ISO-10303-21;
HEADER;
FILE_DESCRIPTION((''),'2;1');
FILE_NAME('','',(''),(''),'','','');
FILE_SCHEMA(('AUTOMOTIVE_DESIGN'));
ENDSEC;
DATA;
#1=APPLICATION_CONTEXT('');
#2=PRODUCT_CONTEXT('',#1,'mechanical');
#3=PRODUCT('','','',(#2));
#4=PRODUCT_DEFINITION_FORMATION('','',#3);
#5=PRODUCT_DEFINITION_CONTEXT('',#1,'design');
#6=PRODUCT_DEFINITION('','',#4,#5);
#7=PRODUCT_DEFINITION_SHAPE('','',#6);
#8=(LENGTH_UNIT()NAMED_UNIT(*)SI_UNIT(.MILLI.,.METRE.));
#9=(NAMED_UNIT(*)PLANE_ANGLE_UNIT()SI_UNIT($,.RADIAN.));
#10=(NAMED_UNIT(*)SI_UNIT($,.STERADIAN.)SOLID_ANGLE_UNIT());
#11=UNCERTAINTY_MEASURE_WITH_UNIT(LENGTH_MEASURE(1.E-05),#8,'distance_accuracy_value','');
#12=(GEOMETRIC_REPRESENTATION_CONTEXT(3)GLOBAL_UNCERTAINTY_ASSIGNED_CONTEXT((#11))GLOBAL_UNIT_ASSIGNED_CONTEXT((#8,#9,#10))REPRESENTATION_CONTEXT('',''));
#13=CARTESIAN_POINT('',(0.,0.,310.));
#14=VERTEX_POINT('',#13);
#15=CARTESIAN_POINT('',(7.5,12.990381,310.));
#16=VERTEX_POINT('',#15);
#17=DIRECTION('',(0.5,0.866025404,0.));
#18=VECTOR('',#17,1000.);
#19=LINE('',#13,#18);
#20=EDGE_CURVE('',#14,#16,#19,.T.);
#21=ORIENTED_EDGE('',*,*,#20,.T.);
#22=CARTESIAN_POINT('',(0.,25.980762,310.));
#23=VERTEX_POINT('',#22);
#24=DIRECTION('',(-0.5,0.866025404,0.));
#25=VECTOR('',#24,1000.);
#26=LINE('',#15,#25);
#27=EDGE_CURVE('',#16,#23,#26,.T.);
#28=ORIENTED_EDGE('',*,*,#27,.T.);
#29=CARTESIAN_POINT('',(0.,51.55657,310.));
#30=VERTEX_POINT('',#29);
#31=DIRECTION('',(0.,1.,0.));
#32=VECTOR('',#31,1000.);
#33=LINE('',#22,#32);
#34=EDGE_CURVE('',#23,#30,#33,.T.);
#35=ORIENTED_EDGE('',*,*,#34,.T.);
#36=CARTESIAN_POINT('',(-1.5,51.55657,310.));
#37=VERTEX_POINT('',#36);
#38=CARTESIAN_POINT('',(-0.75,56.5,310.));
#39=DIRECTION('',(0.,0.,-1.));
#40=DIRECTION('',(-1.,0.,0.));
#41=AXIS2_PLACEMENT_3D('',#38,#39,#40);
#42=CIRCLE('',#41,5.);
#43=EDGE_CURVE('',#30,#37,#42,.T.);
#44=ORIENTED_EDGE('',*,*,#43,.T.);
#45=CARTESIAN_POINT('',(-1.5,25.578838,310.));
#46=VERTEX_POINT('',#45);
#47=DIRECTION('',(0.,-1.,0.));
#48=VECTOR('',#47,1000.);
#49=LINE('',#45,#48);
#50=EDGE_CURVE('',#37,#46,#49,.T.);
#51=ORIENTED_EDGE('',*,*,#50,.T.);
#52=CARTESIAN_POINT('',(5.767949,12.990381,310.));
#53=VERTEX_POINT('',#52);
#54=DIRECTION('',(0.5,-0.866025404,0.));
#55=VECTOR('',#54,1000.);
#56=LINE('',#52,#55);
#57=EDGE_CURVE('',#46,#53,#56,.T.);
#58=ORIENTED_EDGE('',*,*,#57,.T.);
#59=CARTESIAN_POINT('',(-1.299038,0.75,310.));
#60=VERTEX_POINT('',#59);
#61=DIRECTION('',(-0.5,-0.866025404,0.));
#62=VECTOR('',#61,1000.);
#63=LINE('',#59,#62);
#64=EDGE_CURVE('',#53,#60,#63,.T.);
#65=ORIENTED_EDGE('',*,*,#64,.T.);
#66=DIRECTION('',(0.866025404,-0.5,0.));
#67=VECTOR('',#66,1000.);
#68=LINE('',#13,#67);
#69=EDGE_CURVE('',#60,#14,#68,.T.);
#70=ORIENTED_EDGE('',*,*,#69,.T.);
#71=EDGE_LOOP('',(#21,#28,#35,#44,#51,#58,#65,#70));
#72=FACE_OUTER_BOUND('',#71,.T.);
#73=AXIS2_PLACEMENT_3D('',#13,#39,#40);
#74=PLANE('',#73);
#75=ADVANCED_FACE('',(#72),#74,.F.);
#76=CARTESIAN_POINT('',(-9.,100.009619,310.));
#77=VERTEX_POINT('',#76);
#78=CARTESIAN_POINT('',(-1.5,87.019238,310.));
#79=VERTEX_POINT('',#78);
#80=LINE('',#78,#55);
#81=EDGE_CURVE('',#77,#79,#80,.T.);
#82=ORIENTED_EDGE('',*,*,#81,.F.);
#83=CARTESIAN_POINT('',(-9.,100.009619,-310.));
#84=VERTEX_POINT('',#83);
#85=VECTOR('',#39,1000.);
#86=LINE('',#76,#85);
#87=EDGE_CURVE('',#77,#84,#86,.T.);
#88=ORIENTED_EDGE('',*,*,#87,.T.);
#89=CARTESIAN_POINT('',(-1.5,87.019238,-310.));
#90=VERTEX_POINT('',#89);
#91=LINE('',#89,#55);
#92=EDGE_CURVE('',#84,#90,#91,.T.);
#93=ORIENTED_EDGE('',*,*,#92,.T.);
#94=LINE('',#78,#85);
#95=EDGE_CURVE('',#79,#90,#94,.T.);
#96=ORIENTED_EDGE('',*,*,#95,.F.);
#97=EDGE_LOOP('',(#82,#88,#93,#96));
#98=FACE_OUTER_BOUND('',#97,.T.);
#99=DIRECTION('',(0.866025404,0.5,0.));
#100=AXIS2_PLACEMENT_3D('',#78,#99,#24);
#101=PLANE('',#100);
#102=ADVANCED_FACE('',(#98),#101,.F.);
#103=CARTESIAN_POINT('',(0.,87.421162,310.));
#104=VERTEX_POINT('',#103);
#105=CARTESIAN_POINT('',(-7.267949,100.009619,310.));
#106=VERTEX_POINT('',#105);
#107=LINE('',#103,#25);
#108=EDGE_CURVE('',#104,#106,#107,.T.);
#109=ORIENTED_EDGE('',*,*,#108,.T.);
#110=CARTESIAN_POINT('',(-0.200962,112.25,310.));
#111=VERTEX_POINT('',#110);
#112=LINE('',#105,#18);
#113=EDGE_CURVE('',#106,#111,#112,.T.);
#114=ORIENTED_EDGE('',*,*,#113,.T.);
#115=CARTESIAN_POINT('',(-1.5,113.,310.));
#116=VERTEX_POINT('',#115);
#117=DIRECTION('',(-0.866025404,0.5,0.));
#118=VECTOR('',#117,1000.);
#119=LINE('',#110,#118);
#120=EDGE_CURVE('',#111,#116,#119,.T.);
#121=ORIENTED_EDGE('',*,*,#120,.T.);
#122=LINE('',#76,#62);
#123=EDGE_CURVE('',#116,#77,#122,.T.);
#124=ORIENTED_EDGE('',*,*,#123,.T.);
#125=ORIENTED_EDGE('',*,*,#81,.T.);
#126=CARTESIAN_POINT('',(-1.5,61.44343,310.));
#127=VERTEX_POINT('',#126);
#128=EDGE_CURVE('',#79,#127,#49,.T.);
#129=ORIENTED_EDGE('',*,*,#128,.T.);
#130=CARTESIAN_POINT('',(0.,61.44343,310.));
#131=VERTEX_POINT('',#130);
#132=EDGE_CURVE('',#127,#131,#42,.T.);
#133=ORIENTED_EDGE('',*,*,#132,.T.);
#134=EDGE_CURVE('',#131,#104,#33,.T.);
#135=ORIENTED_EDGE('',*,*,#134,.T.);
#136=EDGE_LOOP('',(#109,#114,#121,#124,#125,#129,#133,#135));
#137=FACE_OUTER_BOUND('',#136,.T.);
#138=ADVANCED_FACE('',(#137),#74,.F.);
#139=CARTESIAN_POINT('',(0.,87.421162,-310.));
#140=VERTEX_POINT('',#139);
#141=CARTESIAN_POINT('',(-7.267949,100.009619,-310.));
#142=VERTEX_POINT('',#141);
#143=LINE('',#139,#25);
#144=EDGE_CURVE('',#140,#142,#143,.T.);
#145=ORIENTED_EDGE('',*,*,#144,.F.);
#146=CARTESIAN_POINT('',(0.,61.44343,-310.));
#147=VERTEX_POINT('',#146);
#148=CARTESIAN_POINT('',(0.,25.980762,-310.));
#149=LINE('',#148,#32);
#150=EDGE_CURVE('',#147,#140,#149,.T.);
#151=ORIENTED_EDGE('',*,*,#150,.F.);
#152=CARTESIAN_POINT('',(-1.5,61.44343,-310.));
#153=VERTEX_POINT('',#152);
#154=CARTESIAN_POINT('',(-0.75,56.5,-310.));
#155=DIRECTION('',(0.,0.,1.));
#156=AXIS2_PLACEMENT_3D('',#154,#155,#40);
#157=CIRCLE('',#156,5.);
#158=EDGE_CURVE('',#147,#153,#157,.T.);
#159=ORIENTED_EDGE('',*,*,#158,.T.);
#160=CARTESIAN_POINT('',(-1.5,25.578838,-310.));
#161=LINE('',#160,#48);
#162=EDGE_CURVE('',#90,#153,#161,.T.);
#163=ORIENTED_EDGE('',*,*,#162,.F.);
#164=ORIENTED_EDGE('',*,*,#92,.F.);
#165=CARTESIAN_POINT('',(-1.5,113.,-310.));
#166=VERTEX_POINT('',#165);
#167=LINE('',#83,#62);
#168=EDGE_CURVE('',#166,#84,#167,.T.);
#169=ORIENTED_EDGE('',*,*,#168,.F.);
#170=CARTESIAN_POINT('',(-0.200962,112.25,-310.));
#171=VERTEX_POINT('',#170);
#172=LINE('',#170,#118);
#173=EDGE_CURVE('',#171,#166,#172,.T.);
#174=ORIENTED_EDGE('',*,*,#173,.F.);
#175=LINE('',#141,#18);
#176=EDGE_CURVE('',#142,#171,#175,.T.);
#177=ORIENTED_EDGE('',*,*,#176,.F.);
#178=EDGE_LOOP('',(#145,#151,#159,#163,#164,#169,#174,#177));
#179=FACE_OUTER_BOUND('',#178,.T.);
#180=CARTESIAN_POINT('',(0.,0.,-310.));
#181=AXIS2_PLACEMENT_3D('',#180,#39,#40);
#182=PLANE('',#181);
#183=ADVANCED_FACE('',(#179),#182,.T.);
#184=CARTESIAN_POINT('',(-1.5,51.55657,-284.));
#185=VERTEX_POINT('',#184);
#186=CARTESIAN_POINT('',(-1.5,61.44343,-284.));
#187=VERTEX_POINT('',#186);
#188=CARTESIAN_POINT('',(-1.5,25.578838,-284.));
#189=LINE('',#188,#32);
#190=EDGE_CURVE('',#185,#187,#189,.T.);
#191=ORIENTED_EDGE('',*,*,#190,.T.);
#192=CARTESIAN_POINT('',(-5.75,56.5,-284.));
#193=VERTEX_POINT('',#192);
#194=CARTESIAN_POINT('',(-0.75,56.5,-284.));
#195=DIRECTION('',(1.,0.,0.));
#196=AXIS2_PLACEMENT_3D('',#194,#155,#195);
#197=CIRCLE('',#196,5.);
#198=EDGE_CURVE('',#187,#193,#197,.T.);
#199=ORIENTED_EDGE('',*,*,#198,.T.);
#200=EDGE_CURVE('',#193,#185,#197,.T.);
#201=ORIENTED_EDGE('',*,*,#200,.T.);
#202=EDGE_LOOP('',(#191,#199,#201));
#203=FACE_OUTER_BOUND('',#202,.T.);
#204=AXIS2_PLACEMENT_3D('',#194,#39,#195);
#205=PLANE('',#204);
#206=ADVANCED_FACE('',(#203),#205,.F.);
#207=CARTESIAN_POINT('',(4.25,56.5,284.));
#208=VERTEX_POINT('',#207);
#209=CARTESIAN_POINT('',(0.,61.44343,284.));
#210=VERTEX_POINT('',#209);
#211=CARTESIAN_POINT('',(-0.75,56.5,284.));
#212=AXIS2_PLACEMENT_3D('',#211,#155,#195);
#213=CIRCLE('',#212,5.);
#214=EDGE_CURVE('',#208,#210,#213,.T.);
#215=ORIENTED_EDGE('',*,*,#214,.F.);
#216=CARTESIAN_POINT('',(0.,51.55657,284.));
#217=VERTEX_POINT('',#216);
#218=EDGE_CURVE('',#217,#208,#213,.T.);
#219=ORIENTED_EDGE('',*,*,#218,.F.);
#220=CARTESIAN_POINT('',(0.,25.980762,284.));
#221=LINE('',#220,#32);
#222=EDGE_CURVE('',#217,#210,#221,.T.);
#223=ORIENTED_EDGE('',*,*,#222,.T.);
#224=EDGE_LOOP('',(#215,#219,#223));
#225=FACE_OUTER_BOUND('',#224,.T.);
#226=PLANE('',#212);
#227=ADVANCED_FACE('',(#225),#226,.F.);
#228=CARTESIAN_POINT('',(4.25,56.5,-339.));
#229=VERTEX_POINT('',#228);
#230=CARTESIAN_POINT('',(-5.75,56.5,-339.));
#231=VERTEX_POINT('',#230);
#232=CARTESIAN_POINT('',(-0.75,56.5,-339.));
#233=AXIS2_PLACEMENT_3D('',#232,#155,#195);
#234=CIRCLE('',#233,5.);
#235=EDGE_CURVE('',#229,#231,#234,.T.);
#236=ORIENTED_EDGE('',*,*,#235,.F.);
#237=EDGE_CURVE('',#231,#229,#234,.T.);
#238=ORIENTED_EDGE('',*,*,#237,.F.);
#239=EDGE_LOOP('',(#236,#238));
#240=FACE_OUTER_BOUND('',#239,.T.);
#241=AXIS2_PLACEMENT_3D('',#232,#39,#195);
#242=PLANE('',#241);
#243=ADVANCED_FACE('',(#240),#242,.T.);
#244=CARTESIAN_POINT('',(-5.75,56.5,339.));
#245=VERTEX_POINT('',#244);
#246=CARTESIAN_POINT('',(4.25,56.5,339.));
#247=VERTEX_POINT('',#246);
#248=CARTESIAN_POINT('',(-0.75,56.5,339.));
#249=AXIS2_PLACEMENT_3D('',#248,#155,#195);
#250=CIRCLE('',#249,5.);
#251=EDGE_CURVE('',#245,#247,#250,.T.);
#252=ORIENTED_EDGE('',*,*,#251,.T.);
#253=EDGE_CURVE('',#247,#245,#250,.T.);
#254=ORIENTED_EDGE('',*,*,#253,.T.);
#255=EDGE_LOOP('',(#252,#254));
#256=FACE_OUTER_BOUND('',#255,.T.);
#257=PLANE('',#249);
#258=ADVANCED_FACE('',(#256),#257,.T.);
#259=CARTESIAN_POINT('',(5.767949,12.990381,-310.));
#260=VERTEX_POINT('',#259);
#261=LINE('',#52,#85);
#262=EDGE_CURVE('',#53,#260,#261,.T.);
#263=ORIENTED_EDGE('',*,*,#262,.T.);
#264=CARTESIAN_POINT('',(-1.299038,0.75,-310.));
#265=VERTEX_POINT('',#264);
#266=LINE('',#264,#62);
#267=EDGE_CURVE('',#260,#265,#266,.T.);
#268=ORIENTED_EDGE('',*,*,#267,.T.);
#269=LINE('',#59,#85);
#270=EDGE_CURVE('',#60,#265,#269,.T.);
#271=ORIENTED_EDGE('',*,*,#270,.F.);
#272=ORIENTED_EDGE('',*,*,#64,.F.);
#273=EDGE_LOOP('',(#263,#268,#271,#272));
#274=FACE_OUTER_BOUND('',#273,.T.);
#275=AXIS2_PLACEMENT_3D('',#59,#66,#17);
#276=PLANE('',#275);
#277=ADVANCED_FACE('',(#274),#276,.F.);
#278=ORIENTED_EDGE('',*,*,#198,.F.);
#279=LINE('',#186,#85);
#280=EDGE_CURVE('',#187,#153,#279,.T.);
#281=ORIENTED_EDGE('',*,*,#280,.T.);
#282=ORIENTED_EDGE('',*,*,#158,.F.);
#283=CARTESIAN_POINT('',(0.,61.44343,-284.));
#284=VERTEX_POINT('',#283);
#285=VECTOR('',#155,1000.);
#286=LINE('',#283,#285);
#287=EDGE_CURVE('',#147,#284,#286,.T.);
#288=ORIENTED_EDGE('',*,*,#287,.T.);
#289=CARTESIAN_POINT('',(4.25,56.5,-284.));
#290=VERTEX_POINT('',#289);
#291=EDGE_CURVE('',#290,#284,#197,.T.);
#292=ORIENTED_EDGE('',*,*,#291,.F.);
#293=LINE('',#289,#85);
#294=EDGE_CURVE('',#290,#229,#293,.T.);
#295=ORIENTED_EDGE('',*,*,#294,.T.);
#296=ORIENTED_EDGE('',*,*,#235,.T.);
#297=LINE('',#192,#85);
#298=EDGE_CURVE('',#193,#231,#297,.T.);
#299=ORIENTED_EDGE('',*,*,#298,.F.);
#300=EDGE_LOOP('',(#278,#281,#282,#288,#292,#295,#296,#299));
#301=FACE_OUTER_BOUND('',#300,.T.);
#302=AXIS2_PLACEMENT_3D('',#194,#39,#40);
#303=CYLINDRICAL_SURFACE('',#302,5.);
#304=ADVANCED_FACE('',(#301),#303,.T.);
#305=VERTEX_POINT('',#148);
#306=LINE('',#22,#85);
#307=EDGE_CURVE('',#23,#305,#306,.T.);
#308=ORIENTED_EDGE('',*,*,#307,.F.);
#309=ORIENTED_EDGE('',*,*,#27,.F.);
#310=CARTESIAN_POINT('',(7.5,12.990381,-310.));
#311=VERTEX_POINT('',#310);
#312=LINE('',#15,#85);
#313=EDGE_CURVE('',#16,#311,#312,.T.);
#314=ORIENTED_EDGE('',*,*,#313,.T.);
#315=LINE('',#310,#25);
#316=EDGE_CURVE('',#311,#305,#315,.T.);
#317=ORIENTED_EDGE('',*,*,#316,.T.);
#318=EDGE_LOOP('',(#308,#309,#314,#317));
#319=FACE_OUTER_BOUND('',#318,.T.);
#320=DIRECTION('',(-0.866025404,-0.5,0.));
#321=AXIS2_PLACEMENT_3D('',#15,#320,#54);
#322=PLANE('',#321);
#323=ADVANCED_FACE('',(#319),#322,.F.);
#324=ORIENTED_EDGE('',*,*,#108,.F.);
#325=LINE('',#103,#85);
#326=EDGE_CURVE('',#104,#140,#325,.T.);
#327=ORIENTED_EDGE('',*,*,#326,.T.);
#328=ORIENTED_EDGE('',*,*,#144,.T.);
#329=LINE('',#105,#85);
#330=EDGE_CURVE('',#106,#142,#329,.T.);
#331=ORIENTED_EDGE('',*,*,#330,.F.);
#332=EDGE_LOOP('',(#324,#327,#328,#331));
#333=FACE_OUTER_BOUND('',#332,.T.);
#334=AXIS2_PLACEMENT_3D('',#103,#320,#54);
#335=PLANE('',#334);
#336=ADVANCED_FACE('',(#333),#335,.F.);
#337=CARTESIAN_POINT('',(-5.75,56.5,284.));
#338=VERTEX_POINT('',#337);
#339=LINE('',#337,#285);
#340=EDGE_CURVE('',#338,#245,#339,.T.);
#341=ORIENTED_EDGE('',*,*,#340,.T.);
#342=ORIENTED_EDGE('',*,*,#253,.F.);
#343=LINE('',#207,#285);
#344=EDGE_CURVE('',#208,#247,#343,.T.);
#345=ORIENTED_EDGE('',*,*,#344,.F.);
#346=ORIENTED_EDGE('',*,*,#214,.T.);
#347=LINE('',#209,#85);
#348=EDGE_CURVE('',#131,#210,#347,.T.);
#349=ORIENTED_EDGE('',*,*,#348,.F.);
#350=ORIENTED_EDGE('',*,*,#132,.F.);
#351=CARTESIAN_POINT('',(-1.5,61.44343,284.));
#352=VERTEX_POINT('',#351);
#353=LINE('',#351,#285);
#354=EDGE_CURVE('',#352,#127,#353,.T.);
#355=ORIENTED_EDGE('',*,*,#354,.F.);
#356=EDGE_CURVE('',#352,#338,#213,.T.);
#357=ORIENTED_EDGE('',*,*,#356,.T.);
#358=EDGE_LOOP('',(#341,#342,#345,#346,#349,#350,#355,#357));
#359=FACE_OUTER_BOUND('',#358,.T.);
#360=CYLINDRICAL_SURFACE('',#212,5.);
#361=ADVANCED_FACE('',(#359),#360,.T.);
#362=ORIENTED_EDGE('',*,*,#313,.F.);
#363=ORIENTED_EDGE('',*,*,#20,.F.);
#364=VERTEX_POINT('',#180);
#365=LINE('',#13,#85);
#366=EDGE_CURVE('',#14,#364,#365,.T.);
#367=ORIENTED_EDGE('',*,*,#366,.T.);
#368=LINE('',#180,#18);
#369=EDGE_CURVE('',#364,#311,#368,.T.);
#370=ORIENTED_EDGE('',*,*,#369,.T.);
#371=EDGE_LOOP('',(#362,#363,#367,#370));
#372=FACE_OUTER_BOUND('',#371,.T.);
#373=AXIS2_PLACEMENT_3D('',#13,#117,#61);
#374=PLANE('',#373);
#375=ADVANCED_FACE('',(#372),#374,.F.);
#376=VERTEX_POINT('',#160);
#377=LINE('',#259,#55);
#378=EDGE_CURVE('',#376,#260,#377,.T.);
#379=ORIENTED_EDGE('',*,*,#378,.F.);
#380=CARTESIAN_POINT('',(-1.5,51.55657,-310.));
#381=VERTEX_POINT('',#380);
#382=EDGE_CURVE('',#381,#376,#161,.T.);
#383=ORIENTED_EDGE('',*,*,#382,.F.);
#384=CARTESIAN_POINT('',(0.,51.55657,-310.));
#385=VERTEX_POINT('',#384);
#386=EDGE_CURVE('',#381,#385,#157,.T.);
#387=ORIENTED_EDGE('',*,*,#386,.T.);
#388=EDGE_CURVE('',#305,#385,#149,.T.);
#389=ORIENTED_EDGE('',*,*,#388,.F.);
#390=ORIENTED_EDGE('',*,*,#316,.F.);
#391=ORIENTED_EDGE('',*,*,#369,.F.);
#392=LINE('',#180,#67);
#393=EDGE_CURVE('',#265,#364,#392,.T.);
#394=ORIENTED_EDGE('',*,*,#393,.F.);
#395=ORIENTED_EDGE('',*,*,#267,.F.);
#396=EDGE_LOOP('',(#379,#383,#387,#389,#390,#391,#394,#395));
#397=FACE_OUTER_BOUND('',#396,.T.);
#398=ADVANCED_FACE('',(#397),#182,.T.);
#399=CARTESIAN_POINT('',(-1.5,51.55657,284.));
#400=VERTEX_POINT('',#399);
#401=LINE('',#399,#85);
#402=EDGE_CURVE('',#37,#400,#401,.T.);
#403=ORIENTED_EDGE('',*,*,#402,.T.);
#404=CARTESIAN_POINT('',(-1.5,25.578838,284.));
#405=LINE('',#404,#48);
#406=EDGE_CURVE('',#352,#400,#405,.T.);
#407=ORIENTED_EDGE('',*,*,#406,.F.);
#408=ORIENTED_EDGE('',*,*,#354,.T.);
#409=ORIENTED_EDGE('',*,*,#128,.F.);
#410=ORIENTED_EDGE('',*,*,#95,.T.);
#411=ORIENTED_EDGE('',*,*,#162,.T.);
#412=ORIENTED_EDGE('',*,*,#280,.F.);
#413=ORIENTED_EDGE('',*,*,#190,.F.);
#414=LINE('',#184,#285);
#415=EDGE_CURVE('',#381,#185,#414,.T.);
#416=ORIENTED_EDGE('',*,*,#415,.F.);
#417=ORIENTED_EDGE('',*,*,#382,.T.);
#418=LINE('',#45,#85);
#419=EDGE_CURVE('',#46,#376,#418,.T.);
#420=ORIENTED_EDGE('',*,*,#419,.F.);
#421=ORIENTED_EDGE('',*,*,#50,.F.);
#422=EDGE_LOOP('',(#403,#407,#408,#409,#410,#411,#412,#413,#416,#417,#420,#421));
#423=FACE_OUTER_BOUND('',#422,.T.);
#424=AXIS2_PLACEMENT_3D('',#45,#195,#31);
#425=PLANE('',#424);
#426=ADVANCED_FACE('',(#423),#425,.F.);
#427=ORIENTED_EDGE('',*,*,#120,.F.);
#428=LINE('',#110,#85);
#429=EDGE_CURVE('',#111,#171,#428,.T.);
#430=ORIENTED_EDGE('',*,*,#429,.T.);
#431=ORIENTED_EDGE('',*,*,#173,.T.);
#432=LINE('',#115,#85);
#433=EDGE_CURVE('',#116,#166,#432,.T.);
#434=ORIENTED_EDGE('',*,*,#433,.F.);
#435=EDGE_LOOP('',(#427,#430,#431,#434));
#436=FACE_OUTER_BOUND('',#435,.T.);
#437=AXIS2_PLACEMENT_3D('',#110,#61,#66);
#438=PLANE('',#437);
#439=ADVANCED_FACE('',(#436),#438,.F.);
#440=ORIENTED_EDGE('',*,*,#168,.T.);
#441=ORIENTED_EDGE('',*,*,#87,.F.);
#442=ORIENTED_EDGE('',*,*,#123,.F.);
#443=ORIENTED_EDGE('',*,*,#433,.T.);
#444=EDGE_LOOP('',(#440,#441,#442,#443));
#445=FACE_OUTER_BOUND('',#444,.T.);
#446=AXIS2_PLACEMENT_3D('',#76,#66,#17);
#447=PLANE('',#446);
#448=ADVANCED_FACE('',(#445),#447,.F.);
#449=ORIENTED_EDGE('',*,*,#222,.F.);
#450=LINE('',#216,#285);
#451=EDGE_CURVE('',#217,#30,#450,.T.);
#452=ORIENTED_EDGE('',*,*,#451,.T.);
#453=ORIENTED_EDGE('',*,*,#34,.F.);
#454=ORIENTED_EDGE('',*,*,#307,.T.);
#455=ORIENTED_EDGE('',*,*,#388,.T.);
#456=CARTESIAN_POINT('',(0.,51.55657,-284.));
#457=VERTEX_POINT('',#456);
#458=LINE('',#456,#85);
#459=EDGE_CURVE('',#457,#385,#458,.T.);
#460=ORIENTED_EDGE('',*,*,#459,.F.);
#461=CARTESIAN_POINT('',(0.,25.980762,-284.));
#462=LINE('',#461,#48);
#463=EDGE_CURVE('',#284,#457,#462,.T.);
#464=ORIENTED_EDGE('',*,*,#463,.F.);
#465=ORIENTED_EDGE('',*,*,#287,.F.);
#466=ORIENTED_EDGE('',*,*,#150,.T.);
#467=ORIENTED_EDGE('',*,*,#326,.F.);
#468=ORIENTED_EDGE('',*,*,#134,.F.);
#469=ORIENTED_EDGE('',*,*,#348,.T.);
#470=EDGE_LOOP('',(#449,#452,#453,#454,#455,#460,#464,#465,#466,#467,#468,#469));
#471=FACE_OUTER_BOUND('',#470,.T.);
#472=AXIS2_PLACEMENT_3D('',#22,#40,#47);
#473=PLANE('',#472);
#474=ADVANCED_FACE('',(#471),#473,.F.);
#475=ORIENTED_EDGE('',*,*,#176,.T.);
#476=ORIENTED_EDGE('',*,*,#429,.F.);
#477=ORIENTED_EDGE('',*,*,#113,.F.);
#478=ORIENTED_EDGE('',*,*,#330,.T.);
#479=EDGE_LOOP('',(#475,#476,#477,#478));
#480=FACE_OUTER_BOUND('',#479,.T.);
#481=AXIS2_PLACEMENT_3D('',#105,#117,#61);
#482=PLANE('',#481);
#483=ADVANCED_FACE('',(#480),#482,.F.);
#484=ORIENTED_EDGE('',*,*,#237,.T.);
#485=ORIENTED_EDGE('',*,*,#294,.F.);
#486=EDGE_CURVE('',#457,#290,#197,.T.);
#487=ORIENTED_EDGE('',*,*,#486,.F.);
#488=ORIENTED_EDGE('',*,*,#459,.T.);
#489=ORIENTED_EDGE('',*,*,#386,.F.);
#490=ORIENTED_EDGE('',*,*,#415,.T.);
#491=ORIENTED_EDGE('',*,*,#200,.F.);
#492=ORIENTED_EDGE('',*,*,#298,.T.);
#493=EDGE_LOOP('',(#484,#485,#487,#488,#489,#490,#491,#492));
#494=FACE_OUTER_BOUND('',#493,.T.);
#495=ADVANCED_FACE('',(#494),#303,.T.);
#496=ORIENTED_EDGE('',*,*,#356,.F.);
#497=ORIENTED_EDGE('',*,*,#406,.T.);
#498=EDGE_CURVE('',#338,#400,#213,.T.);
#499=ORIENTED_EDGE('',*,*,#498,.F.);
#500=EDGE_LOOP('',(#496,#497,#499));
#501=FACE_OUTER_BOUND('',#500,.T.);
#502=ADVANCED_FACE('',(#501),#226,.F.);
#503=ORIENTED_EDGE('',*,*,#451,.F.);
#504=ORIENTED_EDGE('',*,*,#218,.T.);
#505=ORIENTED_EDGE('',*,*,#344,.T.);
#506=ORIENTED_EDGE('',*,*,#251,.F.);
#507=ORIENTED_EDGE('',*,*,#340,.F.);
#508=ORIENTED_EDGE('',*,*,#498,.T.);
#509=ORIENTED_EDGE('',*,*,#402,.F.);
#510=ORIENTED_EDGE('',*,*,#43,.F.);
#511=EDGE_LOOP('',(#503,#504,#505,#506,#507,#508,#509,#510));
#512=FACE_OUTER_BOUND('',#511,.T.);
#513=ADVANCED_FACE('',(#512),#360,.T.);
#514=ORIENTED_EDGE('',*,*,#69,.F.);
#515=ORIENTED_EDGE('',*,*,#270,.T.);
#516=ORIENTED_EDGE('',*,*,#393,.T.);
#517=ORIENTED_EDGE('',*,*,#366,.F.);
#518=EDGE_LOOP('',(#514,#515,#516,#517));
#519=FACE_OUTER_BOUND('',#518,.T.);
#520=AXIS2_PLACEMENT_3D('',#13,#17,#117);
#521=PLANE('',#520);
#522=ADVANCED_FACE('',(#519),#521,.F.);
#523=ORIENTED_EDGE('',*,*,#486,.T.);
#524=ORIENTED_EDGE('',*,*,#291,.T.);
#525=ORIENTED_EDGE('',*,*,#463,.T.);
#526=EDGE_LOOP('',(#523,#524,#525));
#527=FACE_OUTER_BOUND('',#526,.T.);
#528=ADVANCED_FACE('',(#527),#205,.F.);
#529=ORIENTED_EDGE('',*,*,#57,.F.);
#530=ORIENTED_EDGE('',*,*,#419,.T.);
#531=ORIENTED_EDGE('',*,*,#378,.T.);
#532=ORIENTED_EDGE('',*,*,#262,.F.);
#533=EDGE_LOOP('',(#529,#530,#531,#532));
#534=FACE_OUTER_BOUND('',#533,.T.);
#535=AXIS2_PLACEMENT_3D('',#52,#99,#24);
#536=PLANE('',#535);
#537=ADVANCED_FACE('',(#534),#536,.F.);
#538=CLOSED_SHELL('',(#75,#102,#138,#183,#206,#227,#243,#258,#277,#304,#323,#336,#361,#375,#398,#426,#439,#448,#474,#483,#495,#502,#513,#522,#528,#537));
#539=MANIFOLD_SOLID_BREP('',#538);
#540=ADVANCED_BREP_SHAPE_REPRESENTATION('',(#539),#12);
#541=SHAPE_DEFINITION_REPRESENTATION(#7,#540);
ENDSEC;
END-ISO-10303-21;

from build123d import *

# Parameters (mm, degrees)
BOSS_EXTRUDE1_DEPTH = 310
BOSS_EXTRUDE2_START = -26
SKETCH2_R           = 5
BOSS_EXTRUDE2_DEPTH = 55


with BuildPart() as part:
    # Sketch1 → Boss-Extrude1 (new, symmetric)
    with BuildSketch(Plane.XY):
        Polygon((0, 0), (7.5, 12.990381057), (0, 25.980762114), (0, 87.421161675), (-7.267949192, 100.009618943), (-0.200961894, 112.25), (-1.5, 113), (-9, 100.009618943), (-1.5, 87.019237886), (-1.5, 25.578838325), (5.767949192, 12.990381057), (-1.299038106, 0.75), align=None)
    extrude(amount=BOSS_EXTRUDE1_DEPTH, both=True)

    # Sketch2 → Boss-Extrude2 (add)
    with BuildSketch(Plane.XY.offset(310).offset(BOSS_EXTRUDE2_START)):
        with Locations((-0.75, 56.5)):
            Circle(SKETCH2_R)
    boss_extrude2 = extrude(amount=BOSS_EXTRUDE2_DEPTH)

    # Mirror1: Boss-Extrude2 across plane
    add(boss_extrude2.mirror(Plane.XY))


solid = part.part
